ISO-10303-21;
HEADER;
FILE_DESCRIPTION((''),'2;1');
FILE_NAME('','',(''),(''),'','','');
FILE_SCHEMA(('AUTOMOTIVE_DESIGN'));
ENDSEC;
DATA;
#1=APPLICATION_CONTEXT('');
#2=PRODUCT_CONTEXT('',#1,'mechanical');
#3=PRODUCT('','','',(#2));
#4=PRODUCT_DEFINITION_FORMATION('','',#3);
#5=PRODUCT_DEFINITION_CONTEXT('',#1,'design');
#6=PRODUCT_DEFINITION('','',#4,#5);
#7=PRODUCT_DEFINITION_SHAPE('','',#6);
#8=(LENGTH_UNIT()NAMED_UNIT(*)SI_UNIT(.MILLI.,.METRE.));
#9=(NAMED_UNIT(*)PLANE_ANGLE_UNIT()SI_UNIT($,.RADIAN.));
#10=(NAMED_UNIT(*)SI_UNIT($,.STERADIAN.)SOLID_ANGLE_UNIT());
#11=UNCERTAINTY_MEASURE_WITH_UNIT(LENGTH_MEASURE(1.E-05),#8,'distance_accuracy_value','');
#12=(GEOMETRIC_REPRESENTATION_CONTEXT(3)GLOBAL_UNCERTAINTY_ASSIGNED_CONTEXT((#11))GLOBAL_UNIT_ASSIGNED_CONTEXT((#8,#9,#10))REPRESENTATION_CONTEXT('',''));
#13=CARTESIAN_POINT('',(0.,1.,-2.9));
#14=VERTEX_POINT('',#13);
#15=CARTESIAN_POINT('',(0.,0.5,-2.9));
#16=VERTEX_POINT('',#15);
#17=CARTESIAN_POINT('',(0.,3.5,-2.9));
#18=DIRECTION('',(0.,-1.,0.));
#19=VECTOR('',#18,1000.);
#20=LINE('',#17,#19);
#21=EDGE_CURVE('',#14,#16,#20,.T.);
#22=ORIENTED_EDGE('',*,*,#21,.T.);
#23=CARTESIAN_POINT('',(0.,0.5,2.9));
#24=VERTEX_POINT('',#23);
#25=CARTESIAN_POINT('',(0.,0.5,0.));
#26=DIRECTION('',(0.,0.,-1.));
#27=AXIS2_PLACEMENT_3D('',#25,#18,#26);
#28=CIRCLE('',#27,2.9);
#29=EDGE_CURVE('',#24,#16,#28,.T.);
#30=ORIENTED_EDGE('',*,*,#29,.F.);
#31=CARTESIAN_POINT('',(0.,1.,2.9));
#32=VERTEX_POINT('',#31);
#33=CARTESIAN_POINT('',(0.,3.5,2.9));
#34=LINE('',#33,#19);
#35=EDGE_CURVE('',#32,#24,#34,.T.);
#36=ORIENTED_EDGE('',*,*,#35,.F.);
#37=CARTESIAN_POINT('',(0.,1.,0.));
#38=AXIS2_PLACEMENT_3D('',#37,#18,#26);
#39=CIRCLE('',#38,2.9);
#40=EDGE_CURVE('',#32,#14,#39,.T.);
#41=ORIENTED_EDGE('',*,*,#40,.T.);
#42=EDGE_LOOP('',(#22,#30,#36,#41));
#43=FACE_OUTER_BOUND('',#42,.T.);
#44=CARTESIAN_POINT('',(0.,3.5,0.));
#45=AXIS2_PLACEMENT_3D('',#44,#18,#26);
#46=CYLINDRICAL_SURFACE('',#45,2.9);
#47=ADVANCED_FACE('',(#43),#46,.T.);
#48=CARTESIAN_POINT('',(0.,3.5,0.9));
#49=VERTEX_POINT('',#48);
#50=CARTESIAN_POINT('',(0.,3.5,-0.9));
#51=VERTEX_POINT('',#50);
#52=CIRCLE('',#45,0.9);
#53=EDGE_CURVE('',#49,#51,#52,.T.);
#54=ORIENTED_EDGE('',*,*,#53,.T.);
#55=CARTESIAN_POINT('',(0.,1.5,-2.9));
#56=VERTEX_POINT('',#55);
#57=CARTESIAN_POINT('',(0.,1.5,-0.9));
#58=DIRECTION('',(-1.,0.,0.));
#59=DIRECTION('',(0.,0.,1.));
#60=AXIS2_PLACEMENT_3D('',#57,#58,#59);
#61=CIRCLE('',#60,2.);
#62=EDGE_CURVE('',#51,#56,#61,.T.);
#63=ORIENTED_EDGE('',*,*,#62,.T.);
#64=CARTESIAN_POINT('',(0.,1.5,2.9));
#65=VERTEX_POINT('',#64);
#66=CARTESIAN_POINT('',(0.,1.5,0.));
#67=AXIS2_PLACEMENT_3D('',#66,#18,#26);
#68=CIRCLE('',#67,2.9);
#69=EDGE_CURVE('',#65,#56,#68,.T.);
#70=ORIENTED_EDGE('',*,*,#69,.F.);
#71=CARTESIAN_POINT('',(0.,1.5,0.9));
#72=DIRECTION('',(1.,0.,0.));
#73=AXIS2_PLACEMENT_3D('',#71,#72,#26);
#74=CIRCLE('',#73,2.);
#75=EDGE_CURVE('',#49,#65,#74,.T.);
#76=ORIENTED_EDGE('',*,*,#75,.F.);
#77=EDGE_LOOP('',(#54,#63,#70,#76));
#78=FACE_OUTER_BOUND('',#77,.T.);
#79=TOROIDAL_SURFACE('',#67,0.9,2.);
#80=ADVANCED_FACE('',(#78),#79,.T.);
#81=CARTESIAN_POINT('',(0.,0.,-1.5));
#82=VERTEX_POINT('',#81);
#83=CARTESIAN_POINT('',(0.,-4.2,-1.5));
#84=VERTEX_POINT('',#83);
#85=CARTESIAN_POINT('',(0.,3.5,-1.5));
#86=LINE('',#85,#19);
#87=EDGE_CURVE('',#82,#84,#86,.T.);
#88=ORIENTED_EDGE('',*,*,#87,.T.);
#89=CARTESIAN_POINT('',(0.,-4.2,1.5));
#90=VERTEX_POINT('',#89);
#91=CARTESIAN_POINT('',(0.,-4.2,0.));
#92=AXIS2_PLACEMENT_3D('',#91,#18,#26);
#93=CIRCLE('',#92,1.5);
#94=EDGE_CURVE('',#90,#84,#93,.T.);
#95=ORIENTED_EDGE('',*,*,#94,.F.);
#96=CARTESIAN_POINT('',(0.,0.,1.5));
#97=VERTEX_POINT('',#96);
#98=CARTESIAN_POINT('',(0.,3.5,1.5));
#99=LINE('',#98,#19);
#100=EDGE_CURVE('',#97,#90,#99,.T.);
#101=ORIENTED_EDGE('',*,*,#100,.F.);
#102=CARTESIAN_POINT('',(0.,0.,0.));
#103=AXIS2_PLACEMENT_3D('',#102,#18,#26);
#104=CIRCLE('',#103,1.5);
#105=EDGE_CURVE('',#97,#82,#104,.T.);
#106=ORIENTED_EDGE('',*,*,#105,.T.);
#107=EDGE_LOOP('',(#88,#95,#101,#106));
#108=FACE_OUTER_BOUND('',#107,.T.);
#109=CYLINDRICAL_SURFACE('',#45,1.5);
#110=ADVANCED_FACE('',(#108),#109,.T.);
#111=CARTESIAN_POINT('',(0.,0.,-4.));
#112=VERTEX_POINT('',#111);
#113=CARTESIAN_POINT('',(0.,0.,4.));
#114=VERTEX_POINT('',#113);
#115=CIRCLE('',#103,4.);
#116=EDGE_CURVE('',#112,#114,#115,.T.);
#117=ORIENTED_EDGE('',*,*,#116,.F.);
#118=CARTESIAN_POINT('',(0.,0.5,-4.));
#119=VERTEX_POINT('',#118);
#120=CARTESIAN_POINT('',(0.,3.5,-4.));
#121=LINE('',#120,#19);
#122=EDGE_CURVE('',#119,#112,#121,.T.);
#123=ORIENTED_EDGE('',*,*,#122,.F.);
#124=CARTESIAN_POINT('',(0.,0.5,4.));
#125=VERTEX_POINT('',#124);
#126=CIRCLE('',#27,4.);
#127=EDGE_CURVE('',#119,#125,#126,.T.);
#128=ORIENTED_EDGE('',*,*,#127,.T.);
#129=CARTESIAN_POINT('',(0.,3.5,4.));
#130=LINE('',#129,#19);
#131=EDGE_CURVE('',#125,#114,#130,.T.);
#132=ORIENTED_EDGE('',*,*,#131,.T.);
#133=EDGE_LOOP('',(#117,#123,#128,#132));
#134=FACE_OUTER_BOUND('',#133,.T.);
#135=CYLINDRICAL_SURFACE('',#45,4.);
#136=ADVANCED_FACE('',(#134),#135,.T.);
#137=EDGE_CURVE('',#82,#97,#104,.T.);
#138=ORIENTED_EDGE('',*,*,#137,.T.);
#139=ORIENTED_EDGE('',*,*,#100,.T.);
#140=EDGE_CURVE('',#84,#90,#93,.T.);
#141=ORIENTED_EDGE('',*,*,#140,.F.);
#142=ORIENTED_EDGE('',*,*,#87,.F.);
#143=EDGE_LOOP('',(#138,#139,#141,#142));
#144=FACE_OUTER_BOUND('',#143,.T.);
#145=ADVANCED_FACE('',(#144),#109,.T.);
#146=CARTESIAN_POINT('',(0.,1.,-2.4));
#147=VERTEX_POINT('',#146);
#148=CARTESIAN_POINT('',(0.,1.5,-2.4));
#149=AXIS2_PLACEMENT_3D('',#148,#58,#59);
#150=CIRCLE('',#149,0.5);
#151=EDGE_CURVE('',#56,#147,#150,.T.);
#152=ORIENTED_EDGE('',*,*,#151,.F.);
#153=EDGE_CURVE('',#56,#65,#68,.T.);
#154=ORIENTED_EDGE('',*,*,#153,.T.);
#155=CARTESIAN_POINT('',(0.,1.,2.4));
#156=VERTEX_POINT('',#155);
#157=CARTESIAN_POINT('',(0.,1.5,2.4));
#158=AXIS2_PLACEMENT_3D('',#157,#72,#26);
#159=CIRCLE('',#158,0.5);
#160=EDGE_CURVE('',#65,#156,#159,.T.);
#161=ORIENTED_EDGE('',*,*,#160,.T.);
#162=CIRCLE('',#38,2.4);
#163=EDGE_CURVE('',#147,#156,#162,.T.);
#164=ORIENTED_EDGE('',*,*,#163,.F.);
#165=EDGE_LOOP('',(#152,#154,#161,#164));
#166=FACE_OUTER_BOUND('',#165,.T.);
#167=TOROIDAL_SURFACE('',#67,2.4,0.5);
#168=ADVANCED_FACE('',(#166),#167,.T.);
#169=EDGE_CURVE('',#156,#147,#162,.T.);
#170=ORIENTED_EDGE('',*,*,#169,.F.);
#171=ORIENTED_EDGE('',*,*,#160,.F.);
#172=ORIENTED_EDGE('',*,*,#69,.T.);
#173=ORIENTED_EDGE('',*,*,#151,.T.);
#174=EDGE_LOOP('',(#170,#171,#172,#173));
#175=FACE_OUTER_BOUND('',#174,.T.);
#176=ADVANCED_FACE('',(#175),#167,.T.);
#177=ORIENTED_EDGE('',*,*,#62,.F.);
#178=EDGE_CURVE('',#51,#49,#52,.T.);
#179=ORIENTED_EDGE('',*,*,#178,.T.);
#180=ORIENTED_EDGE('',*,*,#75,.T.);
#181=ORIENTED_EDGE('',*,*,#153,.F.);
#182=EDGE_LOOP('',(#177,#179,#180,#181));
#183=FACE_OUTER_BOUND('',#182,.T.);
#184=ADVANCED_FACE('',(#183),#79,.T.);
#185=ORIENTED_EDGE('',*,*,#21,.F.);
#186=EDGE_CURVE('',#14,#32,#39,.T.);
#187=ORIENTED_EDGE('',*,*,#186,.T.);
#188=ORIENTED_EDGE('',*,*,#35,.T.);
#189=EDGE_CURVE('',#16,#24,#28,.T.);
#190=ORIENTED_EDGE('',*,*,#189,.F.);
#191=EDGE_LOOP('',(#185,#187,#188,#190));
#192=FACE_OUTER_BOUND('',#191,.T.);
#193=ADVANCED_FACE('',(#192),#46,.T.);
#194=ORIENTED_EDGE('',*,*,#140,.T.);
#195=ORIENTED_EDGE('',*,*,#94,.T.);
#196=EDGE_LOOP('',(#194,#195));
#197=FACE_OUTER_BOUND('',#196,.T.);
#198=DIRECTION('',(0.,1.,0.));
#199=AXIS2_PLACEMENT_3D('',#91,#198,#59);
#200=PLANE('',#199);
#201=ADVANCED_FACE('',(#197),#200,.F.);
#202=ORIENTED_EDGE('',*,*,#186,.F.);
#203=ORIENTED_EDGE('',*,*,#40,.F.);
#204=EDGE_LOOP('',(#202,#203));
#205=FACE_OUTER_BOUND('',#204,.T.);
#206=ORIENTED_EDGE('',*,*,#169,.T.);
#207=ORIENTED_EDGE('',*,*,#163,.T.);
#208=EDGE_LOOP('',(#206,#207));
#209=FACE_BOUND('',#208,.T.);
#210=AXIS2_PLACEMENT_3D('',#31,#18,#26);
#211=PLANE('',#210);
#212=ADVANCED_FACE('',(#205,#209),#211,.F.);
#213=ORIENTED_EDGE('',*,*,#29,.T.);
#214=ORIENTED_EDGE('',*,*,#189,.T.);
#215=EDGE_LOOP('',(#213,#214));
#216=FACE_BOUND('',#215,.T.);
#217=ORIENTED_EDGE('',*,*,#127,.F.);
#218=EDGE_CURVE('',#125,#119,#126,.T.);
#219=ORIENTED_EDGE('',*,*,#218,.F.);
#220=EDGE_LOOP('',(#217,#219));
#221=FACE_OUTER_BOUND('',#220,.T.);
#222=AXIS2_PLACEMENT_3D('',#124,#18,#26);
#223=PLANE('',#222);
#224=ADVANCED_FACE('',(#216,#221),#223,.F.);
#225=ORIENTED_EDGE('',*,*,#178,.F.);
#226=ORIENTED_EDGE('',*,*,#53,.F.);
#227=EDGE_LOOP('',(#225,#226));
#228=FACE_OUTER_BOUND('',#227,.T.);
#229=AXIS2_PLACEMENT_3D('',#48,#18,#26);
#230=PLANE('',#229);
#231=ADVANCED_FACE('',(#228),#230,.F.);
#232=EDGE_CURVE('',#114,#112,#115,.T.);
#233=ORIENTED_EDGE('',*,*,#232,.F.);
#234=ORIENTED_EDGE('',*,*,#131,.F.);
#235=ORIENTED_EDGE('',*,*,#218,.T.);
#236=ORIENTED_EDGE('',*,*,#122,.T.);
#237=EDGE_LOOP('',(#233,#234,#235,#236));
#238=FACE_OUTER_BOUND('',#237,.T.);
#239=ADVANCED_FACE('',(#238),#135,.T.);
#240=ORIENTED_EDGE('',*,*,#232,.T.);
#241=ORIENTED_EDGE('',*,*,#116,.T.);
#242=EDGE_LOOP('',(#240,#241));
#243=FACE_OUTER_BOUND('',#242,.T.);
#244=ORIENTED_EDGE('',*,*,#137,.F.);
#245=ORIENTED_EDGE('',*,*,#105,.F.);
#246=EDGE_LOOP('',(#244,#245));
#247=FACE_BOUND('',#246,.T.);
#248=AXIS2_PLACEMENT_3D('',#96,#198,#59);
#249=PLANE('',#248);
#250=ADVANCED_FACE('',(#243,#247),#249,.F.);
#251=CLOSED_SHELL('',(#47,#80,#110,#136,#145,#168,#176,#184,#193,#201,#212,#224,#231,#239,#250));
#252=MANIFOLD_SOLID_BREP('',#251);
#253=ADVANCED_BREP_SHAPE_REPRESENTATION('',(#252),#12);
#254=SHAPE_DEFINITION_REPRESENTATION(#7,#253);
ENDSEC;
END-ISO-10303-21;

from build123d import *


with BuildPart() as part:
    # Sketch1 → Revolve1 (revolve)
    with BuildSketch(Plane(origin=(0, 0, 0), x_dir=(0, 0, -1), z_dir=(1, 0, 0)), mode=Mode.PRIVATE) as revolve1_sk:
        with BuildLine():
            Line((0, -4.2), (-1.5, -4.2))
            Line((-1.5, -4.2), (-1.5, 0))
            Line((-1.5, 0), (-4, 0))
            Line((-4, 0), (-4, 0.5))
            Line((-4, 0.5), (-2.9, 0.5))
            Line((-2.9, 0.5), (-2.9, 1))
            Line((-2.9, 1), (-2.4, 1))
            ThreePointArc((-2.4, 1), (-2.753553391, 1.146446609), (-2.9, 1.5))
            ThreePointArc((-2.9, 1.5), (-2.314213562, 2.914213562), (-0.9, 3.5))
            Line((-0.9, 3.5), (0, 3.5))
            Line((0, 3.5), (0, -4.2))
        make_face()
    revolve(revolve1_sk.sketch.rotate(Axis((0, 3.5, 0), (0, -1, 0)), 180), axis=Axis((0, 3.5, 0), (0, -1, 0)))


solid = part.part
